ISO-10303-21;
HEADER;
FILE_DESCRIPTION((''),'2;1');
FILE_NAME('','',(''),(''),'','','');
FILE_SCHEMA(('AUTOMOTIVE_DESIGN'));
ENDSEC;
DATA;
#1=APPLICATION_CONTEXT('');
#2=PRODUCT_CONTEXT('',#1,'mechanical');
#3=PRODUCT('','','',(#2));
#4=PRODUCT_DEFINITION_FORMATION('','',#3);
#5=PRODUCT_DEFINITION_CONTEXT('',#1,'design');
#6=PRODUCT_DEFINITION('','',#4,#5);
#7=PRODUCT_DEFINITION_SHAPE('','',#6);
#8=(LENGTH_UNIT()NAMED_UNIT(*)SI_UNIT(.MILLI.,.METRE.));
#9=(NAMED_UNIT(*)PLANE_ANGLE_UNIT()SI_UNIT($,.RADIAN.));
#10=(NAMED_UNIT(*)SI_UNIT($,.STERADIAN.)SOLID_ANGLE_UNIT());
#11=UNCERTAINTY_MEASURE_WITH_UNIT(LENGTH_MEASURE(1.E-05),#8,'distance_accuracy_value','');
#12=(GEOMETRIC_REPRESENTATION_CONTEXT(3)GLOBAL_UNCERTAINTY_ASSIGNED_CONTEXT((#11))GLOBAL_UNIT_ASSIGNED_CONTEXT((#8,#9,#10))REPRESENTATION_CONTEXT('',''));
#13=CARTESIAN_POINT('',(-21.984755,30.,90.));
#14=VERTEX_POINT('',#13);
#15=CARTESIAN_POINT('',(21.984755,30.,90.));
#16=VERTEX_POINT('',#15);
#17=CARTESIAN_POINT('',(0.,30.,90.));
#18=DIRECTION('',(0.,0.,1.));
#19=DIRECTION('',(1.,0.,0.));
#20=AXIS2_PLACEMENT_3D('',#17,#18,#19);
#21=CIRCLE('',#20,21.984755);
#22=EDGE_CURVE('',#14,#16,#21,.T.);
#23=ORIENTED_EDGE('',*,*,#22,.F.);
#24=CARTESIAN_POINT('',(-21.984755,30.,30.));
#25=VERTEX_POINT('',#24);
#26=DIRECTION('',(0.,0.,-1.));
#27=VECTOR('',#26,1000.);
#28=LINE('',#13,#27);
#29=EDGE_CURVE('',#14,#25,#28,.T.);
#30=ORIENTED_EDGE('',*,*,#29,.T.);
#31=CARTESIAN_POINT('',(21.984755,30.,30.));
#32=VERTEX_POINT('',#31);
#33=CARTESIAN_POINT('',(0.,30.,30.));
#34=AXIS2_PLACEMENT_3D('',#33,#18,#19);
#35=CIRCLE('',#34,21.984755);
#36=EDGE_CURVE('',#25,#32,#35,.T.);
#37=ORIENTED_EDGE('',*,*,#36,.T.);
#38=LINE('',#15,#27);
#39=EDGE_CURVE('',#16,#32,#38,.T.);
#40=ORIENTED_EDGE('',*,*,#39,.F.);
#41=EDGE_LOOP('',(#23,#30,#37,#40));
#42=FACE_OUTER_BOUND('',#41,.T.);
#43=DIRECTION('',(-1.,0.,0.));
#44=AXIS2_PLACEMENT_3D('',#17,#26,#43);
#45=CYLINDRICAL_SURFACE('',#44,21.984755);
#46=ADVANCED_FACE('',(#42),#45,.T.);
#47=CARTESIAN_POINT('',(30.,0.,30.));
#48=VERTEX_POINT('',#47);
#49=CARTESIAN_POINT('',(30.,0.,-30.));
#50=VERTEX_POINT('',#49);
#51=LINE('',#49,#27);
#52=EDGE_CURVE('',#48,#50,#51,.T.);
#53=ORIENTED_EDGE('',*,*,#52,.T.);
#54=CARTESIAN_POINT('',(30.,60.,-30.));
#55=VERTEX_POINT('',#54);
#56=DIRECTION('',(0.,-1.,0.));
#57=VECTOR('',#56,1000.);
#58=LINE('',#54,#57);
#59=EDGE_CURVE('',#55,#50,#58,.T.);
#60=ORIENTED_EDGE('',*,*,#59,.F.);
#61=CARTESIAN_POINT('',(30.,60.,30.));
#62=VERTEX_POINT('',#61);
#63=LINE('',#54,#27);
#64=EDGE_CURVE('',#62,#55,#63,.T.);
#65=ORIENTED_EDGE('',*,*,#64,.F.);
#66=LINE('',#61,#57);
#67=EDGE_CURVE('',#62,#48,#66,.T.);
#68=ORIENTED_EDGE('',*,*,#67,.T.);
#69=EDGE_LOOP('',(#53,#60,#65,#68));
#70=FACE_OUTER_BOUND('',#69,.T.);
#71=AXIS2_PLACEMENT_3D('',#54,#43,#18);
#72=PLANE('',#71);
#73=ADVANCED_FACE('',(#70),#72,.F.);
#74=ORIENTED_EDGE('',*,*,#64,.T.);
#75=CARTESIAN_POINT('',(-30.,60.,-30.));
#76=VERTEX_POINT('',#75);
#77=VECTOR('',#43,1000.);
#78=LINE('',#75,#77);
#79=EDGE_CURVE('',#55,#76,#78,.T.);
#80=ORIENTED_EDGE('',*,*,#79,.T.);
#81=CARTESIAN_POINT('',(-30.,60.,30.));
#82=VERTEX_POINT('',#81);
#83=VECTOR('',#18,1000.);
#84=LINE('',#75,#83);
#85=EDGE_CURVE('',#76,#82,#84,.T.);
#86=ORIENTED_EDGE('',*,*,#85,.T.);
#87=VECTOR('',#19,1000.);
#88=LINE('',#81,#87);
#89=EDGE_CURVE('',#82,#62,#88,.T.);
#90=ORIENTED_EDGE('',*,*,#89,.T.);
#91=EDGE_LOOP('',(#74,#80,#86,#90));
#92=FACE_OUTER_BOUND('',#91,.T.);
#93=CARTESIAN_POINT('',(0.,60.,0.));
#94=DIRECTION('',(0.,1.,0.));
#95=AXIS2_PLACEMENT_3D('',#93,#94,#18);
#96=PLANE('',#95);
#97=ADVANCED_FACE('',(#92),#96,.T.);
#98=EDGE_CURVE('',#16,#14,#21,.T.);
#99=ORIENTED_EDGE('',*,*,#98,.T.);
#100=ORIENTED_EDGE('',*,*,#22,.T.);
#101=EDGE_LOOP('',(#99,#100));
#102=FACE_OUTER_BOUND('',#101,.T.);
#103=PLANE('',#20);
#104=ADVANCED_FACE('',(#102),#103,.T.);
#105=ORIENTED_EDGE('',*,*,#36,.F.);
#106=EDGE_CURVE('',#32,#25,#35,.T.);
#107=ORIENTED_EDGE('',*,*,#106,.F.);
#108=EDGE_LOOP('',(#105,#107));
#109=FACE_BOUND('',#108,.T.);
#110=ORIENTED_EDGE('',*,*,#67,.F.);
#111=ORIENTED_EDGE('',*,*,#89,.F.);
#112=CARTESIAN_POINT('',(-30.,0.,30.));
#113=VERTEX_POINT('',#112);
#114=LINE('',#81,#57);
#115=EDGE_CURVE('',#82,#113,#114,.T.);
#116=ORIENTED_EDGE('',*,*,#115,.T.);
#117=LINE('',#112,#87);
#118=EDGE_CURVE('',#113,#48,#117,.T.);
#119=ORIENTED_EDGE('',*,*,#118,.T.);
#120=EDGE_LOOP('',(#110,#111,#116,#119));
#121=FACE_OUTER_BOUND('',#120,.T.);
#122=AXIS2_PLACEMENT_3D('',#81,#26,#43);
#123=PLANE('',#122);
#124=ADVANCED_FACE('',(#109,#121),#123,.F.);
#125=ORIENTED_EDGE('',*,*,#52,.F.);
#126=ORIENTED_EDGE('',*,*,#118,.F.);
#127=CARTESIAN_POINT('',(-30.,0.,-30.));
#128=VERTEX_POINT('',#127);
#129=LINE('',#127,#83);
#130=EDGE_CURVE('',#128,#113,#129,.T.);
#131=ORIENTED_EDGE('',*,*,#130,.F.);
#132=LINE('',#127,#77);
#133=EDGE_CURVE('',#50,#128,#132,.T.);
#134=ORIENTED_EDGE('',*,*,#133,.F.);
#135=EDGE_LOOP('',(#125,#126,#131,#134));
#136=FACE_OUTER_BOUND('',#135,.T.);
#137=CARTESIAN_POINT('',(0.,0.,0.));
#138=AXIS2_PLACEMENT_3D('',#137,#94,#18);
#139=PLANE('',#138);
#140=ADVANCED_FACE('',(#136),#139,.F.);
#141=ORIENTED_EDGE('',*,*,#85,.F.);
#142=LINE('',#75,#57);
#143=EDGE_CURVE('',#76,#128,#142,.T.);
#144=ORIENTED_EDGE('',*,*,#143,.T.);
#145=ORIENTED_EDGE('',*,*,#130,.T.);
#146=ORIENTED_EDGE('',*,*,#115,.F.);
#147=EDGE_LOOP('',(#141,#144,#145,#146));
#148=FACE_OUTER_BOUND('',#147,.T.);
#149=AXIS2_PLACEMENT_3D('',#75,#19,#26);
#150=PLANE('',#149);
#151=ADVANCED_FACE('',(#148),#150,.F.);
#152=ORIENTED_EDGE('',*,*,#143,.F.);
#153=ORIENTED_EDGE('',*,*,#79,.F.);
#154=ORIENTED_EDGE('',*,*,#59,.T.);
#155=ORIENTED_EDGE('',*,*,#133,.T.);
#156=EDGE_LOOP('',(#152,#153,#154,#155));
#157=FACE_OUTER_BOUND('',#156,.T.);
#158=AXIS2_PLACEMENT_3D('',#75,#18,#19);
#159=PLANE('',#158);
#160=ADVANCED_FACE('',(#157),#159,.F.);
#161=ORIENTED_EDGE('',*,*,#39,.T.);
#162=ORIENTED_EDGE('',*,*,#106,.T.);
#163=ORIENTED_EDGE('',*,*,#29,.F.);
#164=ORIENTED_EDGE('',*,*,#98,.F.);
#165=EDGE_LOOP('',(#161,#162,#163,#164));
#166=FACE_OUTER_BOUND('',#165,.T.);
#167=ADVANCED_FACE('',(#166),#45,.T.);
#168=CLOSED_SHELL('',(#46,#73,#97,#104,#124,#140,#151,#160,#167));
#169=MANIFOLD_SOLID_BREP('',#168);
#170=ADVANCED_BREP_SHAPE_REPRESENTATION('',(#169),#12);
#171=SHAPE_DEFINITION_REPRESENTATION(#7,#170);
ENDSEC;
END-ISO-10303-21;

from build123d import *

# Parameters (mm, degrees)
SKETCH1_W           = 60
SKETCH1_H           = 60
BOSS_EXTRUDE1_DEPTH = 60
SKETCH2_R           = 21.984754573
BOSS_EXTRUDE2_DEPTH = 60


with BuildPart() as part:
    # Sketch1 → Boss-Extrude1 (new body)
    with BuildSketch(Plane(origin=(0, 0, 0), x_dir=(1, 0, 0), z_dir=(0, 1, 0))):
        Rectangle(SKETCH1_W, SKETCH1_H)
    extrude(amount=BOSS_EXTRUDE1_DEPTH)

    # Sketch2 → Boss-Extrude2 (add)
    with BuildSketch(Plane.XY.offset(30)):
        with Locations((0, 30)):
            Circle(SKETCH2_R)
    extrude(amount=BOSS_EXTRUDE2_DEPTH)


solid = part.part
